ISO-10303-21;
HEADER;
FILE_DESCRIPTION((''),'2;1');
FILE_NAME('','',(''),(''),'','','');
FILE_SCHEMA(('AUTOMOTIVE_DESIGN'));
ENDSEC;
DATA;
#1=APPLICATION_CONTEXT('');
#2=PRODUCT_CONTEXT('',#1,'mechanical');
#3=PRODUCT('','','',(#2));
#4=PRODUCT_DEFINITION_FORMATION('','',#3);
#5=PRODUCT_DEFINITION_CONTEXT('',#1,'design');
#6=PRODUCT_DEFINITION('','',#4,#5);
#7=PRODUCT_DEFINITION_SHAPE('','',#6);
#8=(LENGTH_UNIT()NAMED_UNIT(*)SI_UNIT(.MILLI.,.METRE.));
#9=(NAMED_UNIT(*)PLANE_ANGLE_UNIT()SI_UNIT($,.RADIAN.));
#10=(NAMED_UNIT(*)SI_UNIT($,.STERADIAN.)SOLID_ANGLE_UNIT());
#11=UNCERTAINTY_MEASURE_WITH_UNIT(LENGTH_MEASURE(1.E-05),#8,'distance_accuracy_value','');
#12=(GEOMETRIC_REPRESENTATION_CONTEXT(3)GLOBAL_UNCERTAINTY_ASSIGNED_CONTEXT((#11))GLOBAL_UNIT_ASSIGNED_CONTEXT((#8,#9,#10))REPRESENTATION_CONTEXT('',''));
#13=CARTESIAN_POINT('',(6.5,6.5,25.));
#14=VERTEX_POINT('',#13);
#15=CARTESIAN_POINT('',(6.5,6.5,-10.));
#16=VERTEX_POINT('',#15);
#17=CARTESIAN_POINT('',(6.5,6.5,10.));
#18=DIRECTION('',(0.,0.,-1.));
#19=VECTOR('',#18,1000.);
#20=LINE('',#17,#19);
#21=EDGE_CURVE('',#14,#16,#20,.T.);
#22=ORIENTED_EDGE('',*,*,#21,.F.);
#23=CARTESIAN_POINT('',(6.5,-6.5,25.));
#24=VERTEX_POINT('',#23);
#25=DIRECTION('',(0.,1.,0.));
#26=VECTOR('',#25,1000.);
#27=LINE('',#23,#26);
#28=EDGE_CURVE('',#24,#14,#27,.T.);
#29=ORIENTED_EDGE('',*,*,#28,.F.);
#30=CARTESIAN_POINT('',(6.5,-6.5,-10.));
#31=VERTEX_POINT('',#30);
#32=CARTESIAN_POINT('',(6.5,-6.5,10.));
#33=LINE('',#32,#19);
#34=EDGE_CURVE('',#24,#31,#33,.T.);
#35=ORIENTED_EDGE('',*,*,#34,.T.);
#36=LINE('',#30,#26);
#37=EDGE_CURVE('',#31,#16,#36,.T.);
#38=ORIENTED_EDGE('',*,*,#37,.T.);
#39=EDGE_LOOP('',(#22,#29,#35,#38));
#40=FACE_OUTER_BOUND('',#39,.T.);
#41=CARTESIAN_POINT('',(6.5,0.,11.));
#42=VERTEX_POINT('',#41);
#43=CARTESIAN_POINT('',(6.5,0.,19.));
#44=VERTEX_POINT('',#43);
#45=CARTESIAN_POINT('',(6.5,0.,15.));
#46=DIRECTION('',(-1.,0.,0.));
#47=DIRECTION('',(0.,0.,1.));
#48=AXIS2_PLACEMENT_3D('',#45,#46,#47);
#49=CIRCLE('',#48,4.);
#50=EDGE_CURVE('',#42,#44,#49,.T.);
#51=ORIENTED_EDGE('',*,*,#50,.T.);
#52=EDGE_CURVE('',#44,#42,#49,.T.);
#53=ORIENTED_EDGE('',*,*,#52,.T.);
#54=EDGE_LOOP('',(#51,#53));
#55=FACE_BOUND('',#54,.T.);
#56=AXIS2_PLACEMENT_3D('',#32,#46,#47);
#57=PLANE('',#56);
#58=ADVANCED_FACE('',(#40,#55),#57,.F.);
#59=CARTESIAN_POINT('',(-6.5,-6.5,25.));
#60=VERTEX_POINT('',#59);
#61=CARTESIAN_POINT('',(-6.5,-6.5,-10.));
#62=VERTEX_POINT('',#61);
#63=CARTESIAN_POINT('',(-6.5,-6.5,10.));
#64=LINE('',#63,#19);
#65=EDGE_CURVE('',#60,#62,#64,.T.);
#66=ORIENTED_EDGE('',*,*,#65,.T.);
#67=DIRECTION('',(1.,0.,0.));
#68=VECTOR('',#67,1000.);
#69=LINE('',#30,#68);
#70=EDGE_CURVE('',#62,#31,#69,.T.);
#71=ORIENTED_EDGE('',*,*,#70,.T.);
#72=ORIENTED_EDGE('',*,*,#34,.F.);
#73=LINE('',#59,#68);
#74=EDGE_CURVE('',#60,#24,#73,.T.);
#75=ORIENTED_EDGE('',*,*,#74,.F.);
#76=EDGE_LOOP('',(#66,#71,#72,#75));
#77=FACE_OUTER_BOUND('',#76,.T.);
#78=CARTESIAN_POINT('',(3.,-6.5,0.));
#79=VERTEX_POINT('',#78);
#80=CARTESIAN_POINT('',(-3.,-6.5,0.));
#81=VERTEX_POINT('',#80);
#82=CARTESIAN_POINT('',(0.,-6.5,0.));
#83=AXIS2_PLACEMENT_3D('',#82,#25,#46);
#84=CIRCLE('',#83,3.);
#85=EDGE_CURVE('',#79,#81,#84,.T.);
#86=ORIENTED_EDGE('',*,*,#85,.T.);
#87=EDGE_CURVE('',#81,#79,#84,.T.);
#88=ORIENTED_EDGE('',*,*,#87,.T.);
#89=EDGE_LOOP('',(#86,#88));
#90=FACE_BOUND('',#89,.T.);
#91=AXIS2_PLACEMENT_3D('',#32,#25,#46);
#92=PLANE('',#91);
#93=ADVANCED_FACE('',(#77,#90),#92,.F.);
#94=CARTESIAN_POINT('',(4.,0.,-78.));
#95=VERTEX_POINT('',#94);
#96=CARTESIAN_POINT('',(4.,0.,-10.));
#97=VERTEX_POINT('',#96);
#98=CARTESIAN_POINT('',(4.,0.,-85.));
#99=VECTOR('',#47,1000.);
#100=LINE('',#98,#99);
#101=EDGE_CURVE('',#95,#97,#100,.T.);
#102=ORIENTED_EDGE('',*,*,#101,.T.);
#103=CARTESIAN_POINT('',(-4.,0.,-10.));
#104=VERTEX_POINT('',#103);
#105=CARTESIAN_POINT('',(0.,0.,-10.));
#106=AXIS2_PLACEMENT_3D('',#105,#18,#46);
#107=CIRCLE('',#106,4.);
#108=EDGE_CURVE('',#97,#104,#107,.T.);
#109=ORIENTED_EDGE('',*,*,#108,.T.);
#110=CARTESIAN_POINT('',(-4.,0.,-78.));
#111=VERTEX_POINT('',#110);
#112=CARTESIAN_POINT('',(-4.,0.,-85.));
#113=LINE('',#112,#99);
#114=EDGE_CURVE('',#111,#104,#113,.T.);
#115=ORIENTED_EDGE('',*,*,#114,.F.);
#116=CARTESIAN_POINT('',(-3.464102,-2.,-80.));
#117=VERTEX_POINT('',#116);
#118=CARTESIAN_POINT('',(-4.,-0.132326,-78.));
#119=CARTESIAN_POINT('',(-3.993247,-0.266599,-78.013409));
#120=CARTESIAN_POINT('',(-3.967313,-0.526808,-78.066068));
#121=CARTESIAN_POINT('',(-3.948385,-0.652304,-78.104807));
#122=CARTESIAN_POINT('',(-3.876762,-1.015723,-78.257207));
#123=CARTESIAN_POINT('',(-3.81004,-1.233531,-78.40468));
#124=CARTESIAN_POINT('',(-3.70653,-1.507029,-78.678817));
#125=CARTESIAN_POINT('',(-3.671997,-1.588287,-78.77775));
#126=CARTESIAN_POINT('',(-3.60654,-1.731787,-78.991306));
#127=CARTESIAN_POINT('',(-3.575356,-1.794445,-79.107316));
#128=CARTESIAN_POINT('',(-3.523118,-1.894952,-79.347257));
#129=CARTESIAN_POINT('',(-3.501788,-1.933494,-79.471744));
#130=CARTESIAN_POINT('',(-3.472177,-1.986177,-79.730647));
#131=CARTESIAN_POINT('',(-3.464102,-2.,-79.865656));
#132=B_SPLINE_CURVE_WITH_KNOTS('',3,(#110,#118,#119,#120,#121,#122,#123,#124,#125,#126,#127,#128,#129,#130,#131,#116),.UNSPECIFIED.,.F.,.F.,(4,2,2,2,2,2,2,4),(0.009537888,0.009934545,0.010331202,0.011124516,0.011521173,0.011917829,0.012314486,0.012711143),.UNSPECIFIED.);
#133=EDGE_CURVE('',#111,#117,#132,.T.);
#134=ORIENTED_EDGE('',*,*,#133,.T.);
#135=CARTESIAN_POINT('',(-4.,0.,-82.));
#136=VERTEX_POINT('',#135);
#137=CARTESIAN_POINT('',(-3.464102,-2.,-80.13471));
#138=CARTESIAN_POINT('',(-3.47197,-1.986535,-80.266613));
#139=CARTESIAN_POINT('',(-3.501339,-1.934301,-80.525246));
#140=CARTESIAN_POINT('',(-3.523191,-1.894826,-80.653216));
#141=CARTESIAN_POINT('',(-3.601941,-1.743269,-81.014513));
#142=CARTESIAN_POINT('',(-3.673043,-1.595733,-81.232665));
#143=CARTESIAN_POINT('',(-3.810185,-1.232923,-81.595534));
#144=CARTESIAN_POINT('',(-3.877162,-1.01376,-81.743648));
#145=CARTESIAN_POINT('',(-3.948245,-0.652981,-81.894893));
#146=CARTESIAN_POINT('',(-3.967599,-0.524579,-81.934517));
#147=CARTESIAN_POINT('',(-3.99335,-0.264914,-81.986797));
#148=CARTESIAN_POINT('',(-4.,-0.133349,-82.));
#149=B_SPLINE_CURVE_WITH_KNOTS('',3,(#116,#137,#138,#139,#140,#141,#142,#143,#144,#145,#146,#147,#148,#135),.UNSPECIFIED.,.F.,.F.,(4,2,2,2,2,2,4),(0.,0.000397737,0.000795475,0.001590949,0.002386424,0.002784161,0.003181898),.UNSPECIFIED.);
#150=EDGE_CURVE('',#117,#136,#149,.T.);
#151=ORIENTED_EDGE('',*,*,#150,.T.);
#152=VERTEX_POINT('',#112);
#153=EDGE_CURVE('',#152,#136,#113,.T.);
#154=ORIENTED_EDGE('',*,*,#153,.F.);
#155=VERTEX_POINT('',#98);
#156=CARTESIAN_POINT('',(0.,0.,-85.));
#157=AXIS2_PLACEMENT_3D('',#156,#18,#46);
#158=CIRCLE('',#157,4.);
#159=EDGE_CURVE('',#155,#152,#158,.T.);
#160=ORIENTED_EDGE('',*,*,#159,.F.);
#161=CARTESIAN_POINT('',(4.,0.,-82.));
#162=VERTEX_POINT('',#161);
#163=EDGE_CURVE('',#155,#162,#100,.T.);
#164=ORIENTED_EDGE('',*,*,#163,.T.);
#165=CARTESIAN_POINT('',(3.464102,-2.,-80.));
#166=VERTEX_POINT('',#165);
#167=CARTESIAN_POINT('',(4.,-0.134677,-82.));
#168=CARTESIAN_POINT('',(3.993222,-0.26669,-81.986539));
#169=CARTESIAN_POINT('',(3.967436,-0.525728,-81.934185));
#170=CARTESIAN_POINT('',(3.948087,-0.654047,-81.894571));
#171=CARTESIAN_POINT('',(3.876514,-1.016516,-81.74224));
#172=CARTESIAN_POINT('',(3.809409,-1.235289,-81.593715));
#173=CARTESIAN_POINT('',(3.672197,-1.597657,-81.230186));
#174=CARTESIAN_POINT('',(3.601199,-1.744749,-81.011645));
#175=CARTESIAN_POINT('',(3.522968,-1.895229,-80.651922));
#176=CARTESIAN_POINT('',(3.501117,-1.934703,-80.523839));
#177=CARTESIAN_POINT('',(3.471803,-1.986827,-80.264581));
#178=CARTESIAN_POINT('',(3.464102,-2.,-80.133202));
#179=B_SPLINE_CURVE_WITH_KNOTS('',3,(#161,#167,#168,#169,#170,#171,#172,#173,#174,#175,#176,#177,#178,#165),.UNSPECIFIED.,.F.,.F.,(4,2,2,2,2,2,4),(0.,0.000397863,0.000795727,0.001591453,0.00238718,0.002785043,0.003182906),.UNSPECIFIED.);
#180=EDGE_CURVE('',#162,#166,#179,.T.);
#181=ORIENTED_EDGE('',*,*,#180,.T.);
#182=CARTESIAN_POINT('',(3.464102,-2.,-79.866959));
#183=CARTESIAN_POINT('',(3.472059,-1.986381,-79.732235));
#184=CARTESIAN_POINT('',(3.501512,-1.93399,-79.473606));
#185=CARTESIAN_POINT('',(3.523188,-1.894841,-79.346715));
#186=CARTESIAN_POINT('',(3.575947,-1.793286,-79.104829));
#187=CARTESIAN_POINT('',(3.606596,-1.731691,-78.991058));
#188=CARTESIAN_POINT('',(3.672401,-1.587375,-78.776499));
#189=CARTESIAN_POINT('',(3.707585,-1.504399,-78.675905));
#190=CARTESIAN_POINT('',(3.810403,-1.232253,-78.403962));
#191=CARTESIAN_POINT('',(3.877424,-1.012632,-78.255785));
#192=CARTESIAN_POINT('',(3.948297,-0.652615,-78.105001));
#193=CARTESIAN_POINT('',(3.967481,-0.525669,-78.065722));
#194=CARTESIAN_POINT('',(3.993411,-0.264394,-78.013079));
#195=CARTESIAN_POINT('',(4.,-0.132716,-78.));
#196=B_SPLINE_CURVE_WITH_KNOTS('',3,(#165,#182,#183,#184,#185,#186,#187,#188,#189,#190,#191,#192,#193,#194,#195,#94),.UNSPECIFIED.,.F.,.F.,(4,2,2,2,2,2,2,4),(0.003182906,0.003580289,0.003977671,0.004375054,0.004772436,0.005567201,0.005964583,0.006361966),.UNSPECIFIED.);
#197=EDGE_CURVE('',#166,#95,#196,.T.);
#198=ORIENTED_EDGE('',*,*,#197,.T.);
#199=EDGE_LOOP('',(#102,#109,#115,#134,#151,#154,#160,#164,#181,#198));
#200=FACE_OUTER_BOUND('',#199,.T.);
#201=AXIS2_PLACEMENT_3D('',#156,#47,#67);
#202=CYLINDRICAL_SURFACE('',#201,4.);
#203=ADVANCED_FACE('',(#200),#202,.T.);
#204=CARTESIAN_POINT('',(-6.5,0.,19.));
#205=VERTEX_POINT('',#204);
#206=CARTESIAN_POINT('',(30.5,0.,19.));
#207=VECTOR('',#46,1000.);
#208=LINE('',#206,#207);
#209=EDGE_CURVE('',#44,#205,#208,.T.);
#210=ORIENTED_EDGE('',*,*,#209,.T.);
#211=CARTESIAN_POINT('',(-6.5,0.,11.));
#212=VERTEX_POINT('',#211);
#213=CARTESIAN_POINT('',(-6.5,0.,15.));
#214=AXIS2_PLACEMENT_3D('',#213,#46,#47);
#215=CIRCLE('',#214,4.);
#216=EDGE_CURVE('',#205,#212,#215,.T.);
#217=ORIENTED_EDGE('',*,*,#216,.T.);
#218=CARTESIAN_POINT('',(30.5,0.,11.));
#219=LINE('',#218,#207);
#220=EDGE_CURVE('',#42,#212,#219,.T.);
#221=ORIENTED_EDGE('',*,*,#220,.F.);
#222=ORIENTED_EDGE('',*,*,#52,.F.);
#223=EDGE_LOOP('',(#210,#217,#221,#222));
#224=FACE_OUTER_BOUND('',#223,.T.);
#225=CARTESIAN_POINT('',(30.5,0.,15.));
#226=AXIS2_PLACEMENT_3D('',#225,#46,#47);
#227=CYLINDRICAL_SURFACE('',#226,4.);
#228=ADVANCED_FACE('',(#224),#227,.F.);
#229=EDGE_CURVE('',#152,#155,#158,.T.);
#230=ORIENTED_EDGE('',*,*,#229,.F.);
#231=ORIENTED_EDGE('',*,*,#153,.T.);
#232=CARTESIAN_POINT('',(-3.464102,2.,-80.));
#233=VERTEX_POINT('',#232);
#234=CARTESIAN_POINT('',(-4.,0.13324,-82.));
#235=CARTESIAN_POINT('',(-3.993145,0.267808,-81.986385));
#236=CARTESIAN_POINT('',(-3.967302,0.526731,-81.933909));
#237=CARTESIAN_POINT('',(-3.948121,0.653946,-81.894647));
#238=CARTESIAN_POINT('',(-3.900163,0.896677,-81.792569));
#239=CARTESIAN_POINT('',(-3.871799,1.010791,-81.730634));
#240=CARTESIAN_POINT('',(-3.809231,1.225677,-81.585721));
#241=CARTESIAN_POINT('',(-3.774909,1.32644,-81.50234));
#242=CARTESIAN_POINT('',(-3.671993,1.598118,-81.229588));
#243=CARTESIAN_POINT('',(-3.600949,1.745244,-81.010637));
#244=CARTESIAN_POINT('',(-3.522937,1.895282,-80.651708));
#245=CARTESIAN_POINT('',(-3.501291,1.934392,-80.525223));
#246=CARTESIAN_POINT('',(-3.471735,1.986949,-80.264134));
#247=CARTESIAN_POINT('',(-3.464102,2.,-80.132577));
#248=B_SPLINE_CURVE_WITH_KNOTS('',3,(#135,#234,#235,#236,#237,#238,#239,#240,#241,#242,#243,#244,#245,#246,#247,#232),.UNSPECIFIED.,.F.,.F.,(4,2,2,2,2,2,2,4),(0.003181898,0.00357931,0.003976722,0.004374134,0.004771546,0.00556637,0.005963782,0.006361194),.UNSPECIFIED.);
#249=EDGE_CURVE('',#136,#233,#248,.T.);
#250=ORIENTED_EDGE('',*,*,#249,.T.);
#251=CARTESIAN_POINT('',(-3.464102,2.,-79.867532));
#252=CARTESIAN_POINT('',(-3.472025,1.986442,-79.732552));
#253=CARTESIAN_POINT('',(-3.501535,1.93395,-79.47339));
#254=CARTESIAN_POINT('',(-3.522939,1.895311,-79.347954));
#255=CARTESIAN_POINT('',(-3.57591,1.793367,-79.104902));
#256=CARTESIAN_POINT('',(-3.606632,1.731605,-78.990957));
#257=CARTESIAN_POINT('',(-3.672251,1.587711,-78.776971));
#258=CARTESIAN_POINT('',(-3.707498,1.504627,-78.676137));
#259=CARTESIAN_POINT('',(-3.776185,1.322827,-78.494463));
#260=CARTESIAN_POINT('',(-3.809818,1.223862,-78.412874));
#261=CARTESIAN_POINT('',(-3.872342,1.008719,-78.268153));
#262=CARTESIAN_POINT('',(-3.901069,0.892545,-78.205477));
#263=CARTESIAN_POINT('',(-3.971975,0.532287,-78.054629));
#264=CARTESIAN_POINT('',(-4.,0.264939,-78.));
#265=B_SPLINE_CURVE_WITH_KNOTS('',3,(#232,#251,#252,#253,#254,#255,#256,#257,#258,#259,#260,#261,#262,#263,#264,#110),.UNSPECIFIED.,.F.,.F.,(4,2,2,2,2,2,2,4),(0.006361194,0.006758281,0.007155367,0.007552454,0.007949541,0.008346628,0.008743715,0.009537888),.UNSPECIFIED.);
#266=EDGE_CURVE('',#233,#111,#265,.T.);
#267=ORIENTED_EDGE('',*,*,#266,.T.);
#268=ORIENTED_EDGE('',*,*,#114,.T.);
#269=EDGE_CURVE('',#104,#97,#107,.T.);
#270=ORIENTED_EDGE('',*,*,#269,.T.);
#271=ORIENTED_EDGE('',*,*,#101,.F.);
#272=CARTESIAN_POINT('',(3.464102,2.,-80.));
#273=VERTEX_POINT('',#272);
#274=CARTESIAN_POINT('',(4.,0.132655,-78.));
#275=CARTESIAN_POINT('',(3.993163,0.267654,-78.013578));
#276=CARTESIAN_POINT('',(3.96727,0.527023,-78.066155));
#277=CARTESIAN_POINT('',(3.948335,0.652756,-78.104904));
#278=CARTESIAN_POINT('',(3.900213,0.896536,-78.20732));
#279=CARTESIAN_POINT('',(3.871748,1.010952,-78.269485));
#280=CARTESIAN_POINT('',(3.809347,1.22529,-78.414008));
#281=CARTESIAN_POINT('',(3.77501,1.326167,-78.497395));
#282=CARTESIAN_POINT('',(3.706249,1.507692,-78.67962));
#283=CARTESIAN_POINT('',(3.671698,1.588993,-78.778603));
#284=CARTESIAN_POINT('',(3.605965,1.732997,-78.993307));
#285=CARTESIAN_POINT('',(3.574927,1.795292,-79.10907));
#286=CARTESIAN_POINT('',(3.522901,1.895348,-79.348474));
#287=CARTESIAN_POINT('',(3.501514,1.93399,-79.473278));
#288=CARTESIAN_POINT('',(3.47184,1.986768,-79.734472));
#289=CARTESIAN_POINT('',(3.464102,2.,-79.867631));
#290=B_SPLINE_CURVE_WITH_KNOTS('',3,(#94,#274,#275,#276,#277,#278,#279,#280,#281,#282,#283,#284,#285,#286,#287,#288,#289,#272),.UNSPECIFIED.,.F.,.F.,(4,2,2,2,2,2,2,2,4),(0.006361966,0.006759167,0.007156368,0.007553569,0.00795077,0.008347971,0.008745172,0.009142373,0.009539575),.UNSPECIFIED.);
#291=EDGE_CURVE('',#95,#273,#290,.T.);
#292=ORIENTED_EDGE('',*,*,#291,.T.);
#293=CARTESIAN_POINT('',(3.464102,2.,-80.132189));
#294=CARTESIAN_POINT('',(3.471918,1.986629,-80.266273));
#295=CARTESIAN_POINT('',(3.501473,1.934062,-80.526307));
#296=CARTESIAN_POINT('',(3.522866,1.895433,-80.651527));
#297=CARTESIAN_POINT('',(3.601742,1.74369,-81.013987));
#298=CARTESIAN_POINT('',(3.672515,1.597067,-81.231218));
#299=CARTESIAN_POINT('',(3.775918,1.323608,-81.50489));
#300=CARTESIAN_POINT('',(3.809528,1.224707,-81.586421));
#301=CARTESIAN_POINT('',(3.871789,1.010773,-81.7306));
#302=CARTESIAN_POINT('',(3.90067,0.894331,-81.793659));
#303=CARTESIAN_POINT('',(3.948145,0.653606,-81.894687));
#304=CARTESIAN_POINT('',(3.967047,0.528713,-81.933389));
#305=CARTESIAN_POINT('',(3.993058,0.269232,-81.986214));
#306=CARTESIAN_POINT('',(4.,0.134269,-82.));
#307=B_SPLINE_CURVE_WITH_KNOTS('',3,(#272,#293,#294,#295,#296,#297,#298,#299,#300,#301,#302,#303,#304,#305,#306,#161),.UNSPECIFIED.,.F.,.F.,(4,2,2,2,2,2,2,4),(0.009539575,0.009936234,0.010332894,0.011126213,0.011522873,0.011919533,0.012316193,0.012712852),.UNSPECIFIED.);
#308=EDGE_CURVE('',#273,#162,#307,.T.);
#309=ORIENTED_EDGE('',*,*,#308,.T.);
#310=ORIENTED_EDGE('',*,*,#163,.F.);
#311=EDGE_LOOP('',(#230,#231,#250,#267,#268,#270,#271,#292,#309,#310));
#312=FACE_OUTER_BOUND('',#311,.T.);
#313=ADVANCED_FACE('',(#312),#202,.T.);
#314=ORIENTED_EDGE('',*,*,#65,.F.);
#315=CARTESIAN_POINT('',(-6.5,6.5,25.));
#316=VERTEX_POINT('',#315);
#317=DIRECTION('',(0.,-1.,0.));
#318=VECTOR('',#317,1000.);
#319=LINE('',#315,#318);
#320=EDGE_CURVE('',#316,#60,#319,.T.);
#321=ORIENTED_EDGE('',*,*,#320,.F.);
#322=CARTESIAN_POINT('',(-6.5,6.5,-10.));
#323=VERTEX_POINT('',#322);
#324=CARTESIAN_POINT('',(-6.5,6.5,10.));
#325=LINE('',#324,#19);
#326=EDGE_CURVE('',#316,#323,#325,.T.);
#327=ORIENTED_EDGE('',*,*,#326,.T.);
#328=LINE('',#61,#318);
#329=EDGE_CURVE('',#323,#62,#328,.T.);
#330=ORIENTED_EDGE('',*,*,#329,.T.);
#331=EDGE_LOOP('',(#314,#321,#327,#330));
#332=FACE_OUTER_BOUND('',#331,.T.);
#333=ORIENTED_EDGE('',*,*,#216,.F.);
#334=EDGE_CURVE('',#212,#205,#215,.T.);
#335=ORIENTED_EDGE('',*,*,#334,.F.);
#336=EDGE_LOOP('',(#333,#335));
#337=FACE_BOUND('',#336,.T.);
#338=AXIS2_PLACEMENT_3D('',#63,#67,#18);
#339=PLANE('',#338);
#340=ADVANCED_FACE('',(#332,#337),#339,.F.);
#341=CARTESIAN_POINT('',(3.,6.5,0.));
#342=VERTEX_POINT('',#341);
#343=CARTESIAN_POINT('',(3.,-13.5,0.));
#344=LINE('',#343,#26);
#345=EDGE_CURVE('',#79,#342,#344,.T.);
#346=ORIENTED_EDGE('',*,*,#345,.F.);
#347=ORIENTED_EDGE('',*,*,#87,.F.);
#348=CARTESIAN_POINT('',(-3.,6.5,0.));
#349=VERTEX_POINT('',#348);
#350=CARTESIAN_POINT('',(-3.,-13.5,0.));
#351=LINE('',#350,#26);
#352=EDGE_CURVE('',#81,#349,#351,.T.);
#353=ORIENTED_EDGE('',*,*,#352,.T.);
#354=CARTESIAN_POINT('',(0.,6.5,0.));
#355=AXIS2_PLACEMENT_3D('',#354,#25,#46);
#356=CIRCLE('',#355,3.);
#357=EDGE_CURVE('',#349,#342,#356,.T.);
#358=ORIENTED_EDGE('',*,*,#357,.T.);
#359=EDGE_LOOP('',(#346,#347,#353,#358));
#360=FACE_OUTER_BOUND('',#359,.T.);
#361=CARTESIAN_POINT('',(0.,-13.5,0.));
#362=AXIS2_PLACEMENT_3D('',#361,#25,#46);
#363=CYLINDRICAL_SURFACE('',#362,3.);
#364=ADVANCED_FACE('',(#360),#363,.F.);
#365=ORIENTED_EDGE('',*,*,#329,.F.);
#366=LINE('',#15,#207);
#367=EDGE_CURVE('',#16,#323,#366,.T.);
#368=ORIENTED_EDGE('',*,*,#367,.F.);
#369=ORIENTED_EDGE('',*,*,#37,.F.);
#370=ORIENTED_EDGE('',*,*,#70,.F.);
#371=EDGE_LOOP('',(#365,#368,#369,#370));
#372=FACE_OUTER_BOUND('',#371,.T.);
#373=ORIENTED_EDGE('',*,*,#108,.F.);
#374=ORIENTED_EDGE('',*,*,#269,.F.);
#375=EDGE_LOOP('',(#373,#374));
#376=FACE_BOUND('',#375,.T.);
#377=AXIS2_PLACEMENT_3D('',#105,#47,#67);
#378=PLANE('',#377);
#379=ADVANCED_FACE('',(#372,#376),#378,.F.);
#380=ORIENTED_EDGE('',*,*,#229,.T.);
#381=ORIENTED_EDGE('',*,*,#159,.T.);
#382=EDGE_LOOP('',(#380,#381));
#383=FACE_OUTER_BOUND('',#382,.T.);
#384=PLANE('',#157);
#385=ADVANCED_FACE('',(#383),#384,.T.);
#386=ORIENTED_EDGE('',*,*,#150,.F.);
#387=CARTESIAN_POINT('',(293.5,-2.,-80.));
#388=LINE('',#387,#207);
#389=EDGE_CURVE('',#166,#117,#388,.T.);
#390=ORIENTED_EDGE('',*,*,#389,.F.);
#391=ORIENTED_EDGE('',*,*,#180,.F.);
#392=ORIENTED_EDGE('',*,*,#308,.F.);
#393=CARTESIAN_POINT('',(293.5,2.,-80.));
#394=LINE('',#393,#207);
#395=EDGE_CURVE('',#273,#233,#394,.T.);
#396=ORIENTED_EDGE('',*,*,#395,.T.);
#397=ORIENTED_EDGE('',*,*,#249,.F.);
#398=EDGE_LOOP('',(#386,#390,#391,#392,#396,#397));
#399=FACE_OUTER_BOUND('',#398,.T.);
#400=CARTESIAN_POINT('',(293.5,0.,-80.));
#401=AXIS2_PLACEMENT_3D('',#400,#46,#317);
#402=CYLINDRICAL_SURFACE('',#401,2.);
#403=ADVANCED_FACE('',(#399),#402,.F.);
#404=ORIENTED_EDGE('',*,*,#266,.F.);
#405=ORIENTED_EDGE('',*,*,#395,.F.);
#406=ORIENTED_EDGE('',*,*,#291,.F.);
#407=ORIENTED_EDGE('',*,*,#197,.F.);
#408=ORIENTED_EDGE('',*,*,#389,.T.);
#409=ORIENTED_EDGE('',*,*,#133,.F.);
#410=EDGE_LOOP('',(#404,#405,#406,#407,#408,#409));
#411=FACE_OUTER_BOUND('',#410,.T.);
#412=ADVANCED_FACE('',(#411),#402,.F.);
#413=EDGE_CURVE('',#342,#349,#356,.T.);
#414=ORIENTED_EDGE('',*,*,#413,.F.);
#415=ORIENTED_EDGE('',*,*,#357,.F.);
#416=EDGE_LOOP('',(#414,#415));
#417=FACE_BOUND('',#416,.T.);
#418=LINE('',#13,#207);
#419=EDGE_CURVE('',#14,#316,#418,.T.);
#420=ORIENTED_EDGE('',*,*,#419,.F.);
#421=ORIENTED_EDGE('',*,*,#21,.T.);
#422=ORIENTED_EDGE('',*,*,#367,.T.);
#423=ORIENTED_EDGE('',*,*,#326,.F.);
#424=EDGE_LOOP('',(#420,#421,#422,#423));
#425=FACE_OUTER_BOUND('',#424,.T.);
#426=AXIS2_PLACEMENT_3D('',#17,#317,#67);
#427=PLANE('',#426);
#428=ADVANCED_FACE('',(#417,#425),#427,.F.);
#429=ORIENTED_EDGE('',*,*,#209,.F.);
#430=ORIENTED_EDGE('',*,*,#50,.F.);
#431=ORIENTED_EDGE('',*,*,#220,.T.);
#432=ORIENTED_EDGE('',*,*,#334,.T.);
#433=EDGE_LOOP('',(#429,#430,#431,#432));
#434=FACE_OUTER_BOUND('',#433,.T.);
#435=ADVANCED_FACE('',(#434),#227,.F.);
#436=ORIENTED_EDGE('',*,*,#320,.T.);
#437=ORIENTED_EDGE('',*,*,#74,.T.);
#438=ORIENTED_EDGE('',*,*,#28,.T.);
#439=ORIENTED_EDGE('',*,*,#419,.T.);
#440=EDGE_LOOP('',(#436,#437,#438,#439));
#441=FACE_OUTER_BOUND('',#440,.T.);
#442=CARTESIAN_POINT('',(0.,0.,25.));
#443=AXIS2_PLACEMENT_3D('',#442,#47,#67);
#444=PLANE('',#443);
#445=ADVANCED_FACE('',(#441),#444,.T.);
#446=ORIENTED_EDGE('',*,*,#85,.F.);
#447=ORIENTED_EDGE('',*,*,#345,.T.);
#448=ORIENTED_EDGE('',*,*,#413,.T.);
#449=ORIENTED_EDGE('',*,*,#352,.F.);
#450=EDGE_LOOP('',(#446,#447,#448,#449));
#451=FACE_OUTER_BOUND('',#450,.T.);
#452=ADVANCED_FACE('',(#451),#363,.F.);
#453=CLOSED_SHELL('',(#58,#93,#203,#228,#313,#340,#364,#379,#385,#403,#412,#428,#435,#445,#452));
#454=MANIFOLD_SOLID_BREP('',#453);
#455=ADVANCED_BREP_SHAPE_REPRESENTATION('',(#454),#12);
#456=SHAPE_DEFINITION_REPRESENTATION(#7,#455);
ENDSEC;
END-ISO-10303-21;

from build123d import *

# Parameters (mm, degrees)
SKETCH_1_W          = 13
SKETCH_1_H          = 13
EXTRUDE_1_DEPTH     = 10
SKETCH_3_R          = 3
CUT_EXTRUDE_1_DEPTH = 20
SKETCH_4_R          = 4
EXTRUDE_2_DEPTH     = 75
SKETCH_5_W          = 13
SKETCH_5_H          = 13
EXTRUDE_3_DEPTH     = 15
SKETCH_6_R          = 4
CUT_EXTRUDE_2_DEPTH = 37
SKETCH_7_R          = 2
CUT_EXTRUDE_3_DEPTH = 300


with BuildPart() as part:
    # 草图1 → 凸台-拉伸1 (new, symmetric)
    with BuildSketch(Plane.XY):
        Rectangle(SKETCH_1_W, SKETCH_1_H)
    extrude(amount=EXTRUDE_1_DEPTH, both=True)

    # 草图3 → 切除-拉伸1 (cut)
    with BuildSketch(Plane(origin=(0, 6.5, 0), x_dir=(1, 0, 0), z_dir=(0, 1, 0))):
        with Locations(Location((0, 0, 0), (0, 0, 180))):
            Circle(SKETCH_3_R)
    extrude(amount=-CUT_EXTRUDE_1_DEPTH, mode=Mode.SUBTRACT)

    # 草图4 → 凸台-拉伸2 (add)
    with BuildSketch(Plane(origin=(0, 0, -10), x_dir=(-1, 0, 0), z_dir=(0, 0, -1))):
        Circle(SKETCH_4_R)
    extrude(amount=EXTRUDE_2_DEPTH)

    # 草图5 → 凸台-拉伸3 (add)
    with BuildSketch(Plane.XY.offset(10)):
        Rectangle(SKETCH_5_W, SKETCH_5_H)
    extrude(amount=EXTRUDE_3_DEPTH)

    # 草图6 → 切除-拉伸2 (cut)
    with BuildSketch(Plane.ZY.offset(6.5)):
        with Locations((15, 0)):
            Circle(SKETCH_6_R)
    extrude(amount=-CUT_EXTRUDE_2_DEPTH, mode=Mode.SUBTRACT)

    # 草图7 → 切除-拉伸3 (cut)
    with BuildSketch(Plane.ZY.offset(6.5)):
        with Locations(Location((-80, 0, 0), (0, 0, 179.999999996))):
            Circle(SKETCH_7_R)
    extrude(amount=-CUT_EXTRUDE_3_DEPTH, mode=Mode.SUBTRACT)


solid = part.part
